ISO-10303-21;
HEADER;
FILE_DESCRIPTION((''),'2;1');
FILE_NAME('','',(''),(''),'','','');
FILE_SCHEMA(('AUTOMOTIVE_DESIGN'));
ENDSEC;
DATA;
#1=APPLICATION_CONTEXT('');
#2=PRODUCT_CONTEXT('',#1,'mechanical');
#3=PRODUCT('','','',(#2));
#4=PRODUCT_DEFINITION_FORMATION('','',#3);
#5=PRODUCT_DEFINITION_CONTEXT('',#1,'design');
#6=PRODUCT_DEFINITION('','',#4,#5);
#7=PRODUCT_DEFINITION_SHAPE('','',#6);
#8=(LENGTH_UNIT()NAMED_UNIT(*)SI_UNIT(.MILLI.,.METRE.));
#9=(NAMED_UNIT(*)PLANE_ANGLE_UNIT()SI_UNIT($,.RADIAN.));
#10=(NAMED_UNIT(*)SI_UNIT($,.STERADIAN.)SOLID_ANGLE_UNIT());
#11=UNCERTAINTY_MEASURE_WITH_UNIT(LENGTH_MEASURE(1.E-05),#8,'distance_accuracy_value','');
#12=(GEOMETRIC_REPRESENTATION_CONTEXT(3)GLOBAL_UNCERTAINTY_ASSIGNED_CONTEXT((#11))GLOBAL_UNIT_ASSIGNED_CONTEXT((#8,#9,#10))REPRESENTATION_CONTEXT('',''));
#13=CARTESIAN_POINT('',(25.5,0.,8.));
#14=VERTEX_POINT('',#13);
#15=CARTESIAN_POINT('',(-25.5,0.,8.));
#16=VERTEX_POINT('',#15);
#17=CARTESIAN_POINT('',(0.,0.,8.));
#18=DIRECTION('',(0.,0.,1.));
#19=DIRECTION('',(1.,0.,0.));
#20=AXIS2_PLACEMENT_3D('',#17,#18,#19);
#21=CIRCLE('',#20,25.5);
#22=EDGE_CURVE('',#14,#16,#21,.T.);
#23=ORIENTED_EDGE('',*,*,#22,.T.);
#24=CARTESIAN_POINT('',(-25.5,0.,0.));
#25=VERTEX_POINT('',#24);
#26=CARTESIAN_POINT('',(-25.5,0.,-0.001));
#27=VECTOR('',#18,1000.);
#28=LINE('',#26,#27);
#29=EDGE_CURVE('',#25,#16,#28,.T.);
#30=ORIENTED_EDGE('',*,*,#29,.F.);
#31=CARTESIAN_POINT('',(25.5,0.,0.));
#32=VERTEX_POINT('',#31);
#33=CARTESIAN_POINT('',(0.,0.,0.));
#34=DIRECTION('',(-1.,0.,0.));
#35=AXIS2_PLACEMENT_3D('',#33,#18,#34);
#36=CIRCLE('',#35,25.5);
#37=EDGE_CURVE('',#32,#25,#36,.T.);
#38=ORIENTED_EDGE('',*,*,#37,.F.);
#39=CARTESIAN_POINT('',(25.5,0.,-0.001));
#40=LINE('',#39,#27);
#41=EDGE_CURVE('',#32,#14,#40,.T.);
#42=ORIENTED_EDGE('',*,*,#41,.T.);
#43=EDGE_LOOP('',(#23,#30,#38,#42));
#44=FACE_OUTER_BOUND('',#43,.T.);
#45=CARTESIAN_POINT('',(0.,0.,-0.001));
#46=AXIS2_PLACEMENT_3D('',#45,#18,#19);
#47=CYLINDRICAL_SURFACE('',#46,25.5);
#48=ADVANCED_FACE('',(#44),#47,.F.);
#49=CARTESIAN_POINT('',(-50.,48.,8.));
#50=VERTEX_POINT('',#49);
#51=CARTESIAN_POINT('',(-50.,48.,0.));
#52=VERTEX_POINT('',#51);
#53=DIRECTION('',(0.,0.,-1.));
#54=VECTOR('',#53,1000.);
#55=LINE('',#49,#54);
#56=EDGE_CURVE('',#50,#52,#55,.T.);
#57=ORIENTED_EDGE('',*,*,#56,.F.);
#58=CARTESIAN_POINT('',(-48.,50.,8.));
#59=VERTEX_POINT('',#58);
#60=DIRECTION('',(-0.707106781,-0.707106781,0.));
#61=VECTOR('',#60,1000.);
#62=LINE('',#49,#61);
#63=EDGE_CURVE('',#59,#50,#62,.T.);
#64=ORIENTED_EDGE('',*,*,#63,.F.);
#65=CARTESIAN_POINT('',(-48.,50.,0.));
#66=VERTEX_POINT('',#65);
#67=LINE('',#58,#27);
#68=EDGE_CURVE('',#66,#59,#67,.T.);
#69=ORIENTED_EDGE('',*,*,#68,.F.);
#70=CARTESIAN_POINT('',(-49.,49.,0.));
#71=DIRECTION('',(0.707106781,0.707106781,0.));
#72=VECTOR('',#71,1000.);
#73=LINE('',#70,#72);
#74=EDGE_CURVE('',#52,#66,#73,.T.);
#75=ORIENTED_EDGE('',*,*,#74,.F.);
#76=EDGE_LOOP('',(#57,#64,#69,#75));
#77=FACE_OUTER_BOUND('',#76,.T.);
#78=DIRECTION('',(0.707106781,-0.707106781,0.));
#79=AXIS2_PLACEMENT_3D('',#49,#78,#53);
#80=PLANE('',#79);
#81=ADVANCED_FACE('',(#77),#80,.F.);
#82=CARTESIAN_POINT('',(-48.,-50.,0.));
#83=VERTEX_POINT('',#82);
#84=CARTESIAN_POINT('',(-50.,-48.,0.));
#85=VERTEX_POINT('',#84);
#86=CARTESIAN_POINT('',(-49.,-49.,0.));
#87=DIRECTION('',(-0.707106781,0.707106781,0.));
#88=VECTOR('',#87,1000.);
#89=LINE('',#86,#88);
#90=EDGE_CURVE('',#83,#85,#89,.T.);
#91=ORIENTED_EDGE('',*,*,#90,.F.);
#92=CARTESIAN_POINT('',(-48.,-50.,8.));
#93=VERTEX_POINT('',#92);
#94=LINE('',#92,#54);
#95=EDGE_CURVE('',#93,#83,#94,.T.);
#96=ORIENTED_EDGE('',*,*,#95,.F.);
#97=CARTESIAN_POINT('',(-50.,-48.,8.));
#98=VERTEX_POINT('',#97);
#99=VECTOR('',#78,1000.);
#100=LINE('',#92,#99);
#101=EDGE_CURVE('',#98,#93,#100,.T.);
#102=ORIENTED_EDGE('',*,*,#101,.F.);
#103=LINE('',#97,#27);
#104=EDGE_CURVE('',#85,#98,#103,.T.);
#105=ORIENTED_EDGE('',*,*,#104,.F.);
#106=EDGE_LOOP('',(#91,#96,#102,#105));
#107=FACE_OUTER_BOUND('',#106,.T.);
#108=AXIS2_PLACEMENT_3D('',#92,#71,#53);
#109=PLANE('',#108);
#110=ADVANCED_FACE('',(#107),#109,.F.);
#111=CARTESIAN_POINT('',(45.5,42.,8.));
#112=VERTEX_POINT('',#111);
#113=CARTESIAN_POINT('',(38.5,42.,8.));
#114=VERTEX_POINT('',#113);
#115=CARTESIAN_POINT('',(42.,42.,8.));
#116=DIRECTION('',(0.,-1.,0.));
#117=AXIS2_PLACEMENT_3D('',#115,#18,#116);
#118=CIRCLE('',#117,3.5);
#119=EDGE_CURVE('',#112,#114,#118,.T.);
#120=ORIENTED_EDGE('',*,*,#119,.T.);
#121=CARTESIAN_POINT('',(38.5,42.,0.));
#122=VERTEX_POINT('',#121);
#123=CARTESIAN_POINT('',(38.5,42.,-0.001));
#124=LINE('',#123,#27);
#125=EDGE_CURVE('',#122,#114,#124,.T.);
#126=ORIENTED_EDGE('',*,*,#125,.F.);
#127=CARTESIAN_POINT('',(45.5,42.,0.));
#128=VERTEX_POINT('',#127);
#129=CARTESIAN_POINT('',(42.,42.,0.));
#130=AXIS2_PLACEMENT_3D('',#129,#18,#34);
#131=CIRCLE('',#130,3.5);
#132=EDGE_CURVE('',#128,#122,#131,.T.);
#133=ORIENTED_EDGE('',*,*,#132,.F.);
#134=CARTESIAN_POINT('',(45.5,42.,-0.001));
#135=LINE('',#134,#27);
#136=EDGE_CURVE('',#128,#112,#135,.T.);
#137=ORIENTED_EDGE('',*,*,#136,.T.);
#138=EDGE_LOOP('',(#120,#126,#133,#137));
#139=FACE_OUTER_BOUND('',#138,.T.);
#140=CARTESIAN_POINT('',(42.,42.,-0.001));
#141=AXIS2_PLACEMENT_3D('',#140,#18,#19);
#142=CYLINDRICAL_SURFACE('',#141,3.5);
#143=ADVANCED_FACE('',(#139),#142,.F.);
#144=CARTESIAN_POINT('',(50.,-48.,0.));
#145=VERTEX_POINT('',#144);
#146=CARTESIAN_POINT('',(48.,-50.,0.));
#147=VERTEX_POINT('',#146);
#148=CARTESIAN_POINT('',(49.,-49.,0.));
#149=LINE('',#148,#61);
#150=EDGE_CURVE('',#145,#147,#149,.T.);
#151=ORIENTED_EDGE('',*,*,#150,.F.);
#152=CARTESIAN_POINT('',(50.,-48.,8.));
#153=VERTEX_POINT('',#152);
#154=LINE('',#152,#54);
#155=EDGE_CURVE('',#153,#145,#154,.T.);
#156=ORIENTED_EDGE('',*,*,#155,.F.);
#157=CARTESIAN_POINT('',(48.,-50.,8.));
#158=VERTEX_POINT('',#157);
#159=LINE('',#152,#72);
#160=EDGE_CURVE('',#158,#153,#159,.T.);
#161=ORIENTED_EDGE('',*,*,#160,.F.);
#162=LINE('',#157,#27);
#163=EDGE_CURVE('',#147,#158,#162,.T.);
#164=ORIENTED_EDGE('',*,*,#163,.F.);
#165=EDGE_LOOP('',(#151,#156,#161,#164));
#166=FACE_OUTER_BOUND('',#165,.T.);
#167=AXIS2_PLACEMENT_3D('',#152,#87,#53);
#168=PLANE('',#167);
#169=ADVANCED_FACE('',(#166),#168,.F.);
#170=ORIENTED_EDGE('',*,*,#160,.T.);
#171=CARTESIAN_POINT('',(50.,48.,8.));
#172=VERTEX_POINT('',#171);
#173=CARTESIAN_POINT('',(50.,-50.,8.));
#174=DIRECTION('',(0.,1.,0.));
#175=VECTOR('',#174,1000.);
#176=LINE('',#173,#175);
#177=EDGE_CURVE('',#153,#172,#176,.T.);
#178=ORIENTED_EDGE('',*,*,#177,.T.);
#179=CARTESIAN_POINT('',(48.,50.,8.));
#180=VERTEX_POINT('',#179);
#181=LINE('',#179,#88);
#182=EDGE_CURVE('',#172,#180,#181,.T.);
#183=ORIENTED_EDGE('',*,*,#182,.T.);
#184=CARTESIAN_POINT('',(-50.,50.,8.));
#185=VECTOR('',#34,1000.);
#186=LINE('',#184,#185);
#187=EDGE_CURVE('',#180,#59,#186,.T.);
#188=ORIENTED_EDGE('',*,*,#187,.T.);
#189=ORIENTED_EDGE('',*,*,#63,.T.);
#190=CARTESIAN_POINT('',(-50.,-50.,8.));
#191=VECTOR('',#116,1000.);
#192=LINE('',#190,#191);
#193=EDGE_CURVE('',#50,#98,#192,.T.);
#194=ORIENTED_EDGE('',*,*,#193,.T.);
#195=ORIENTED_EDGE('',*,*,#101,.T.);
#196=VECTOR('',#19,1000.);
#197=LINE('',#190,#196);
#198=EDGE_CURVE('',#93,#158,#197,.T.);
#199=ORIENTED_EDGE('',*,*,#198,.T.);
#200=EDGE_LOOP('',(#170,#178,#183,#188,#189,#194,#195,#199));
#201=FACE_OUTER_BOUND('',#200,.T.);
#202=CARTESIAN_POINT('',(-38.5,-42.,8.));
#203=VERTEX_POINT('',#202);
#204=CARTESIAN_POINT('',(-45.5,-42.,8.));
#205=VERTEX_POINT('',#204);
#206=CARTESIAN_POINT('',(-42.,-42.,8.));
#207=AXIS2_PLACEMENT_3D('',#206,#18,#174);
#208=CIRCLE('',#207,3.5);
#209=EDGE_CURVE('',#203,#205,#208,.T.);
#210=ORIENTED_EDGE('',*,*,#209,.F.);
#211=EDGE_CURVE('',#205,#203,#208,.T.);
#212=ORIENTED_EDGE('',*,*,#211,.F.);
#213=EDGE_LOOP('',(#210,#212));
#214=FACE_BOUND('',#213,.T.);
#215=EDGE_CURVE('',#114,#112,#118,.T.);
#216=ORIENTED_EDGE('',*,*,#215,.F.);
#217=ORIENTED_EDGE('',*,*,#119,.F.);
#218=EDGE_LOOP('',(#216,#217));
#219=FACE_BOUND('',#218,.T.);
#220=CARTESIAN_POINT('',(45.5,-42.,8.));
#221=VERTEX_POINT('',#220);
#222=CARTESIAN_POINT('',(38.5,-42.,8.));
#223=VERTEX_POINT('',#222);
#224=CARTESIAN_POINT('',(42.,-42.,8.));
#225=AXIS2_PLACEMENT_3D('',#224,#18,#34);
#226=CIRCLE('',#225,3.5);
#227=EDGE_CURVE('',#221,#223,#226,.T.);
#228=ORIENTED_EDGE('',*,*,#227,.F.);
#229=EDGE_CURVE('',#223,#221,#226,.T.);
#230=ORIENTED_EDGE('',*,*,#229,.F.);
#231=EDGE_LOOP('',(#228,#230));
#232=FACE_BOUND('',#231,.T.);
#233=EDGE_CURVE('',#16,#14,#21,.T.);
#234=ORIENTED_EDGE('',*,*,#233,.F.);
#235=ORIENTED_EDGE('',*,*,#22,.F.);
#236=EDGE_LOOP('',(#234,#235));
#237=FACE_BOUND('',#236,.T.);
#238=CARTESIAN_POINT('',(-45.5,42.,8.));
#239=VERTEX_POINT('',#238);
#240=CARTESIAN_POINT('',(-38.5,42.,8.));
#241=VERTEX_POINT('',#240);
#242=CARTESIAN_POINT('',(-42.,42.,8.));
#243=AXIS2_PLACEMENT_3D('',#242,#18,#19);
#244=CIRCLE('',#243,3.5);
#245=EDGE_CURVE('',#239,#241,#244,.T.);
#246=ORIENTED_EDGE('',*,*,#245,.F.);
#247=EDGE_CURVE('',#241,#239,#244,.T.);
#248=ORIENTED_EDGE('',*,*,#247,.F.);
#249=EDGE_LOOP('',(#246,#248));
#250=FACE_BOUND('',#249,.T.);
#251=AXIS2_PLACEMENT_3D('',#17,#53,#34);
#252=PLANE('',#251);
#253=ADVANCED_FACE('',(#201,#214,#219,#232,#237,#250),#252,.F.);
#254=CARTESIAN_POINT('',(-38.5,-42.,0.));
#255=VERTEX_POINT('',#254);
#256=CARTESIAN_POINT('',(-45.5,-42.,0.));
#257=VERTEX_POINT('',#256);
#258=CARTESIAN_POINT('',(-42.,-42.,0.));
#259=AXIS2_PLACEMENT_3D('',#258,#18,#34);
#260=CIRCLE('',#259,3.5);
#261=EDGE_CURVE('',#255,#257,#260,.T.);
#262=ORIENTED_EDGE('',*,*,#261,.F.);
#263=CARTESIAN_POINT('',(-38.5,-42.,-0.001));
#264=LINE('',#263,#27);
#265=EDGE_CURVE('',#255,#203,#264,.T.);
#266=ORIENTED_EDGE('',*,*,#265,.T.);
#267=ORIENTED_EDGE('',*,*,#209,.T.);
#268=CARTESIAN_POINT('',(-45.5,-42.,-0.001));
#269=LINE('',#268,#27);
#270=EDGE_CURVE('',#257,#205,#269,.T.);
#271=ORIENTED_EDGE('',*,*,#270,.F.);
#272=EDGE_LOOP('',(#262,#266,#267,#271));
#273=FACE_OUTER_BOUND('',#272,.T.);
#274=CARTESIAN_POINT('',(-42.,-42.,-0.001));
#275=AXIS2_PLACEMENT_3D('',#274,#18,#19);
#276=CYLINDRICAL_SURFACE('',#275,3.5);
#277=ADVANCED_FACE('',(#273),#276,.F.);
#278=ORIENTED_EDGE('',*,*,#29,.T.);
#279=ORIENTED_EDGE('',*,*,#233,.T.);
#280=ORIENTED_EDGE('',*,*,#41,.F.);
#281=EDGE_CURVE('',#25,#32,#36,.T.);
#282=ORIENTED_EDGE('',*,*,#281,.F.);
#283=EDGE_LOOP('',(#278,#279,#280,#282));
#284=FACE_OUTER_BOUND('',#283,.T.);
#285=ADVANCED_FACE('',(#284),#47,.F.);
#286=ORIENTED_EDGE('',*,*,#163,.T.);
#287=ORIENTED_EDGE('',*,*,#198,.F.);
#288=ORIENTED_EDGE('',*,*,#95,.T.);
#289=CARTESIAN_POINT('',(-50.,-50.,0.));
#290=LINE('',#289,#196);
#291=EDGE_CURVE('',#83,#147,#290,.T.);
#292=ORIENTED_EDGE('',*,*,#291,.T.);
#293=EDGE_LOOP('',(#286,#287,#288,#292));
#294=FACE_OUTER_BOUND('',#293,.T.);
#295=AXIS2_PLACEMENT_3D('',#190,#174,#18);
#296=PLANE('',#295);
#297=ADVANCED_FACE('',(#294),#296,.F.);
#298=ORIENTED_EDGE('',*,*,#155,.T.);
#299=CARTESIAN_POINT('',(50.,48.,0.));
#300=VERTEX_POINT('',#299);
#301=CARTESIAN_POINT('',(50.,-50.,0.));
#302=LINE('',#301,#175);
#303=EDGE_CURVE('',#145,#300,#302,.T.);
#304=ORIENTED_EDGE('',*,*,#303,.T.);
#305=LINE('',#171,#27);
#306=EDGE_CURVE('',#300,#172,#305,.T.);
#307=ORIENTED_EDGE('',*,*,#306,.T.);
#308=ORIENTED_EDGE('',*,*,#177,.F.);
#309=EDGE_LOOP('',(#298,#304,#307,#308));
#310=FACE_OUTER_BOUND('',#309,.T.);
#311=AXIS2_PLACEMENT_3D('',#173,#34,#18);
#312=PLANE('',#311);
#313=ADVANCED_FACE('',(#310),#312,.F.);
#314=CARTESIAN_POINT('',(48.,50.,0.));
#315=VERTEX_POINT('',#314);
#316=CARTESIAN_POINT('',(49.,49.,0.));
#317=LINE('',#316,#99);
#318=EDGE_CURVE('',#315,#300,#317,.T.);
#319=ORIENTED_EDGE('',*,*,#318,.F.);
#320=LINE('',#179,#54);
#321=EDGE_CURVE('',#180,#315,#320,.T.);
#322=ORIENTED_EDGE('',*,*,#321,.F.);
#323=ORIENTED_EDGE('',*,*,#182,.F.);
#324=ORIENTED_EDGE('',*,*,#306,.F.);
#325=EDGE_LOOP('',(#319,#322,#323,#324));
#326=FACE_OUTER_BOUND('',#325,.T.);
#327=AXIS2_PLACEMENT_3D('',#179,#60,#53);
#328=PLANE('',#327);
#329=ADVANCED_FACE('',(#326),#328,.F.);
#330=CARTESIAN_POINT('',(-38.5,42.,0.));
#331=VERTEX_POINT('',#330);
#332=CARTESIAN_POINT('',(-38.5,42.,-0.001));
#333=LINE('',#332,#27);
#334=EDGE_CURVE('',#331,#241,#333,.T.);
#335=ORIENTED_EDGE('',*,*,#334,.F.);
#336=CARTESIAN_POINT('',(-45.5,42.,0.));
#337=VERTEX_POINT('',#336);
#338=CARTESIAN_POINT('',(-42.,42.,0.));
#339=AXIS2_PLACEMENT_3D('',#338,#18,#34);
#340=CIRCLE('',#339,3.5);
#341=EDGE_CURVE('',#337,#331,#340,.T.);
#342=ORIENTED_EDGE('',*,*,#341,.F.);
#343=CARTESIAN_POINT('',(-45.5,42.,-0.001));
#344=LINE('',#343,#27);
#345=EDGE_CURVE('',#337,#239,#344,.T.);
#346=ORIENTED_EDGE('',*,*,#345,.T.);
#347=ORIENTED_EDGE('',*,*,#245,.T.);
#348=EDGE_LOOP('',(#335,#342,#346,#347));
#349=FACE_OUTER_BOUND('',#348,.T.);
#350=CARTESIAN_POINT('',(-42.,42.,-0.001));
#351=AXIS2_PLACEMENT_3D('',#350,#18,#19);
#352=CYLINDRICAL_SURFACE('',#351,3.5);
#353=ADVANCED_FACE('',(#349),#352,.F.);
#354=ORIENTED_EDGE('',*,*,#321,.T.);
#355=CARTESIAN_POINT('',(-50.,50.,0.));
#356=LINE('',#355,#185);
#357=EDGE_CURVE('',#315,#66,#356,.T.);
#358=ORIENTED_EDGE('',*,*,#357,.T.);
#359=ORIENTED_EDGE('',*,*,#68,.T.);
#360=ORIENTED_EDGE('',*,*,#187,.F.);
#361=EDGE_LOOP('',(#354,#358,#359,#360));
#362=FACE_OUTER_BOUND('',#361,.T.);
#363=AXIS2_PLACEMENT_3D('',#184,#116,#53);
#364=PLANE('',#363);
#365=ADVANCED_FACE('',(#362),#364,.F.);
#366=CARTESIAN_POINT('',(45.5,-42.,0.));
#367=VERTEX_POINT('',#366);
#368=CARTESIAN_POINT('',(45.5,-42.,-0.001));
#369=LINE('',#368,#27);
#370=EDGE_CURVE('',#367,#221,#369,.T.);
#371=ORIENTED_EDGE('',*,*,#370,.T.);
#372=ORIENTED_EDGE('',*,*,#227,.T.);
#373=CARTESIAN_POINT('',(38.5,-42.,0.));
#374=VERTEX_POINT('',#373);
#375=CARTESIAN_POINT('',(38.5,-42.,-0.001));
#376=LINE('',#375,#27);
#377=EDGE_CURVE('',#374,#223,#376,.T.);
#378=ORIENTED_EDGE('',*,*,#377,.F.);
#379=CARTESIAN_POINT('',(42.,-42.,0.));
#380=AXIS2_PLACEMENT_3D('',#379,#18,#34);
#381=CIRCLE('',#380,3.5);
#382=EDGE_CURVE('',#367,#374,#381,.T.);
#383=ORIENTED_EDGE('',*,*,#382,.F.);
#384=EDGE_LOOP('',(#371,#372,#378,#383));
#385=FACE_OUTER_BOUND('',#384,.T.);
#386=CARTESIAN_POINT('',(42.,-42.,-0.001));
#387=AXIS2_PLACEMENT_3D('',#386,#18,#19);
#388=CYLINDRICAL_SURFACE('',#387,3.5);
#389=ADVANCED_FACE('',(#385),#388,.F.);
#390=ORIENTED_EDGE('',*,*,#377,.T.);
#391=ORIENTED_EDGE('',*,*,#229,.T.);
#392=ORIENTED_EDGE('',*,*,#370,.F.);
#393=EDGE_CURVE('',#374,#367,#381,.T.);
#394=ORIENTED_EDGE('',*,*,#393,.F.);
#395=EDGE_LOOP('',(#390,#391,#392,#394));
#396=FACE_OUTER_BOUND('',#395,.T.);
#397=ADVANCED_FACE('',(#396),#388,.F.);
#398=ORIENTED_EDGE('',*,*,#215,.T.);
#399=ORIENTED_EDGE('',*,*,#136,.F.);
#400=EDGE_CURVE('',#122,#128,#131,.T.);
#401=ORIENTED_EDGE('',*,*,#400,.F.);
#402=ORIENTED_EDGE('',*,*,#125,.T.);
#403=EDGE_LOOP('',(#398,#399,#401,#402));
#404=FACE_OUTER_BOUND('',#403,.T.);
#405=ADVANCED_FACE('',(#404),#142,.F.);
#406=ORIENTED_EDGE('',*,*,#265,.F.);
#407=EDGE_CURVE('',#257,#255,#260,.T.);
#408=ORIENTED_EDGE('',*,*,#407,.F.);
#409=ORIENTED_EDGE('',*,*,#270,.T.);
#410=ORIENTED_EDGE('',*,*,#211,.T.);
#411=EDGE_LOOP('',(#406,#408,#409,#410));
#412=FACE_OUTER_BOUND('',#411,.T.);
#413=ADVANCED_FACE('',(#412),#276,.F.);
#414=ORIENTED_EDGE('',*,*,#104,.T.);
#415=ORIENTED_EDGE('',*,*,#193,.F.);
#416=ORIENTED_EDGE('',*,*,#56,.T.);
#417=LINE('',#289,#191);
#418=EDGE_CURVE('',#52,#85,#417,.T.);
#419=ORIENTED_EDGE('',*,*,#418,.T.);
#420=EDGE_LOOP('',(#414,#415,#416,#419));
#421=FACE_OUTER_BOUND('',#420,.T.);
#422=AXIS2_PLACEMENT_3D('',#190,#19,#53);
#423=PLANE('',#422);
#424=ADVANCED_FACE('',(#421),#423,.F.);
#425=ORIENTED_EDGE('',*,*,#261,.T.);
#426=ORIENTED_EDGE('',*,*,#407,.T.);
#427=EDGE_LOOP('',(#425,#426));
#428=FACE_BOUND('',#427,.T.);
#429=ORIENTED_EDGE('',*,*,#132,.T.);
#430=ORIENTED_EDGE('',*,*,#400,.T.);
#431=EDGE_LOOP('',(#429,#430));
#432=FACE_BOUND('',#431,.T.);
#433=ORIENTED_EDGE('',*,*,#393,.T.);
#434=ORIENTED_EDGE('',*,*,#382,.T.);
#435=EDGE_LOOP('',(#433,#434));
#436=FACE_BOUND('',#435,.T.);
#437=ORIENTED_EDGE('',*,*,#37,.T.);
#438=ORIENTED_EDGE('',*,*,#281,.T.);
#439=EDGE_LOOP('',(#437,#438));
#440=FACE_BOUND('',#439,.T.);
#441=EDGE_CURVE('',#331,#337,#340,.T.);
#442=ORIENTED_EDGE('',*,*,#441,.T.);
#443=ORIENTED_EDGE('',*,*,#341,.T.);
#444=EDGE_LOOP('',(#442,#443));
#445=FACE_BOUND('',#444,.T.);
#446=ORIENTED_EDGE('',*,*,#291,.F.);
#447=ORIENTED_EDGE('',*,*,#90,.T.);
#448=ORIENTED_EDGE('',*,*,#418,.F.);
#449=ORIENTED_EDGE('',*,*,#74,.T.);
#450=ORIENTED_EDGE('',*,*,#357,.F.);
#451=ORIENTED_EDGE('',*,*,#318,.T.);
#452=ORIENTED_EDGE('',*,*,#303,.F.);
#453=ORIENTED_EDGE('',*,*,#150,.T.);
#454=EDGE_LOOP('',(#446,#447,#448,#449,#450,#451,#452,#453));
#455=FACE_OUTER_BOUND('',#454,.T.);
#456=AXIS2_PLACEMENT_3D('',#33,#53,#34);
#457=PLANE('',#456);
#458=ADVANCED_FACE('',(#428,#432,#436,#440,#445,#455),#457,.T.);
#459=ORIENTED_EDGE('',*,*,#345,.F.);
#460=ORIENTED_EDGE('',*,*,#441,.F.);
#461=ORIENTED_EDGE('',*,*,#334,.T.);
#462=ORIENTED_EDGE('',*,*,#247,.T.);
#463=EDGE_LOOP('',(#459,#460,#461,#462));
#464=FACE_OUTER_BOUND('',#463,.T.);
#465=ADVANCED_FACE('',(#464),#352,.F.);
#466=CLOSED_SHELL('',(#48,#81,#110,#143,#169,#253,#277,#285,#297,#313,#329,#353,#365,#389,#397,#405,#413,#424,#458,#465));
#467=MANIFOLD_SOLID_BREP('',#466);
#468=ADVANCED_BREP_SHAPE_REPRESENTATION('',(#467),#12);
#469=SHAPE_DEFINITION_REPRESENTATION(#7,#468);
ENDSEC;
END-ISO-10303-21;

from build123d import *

# Parameters (mm, degrees)
SKETCH_1_W               = 100
SKETCH_1_H               = 100
EXTRUDE_1_DEPTH          = 8
CUT_EXTRUDE_1_REACH      = 73.162
SKETCH_2_R               = 25.5
CUT_EXTRUDE_2_REACH      = 73.162
SKETCH_3_R               = 3.5
PATTERN_CIRCULAR_1_COUNT = 4
CHAMFER_1_SIZE           = 2


with BuildPart() as part:
    # 草图1 → 凸台-拉伸1 (new body)
    with BuildSketch(Plane.XY):
        Rectangle(SKETCH_1_W, SKETCH_1_H)
    extrude(amount=EXTRUDE_1_DEPTH)

    # 草图2 → 切除-拉伸1 (cut, up to next)
    with BuildSketch(Plane.XY.offset(8), mode=Mode.PRIVATE) as cut_extrude_1_sk1:
        Circle(SKETCH_2_R)
    cut_extrude_1_tool1 = extrude(cut_extrude_1_sk1.sketch, amount=-CUT_EXTRUDE_1_REACH, mode=Mode.PRIVATE) & part.part
    add(cut_extrude_1_tool1.solids().sort_by_distance((0, 0, 8))[0], mode=Mode.SUBTRACT)

    # 草图3 → 切除-拉伸2 (cut, up to next)
    with BuildSketch(Plane.XY.offset(8), mode=Mode.PRIVATE) as cut_extrude_2_sk1:
        with Locations((-42, 42)):
            Circle(SKETCH_3_R)
    cut_extrude_2_tool1 = extrude(cut_extrude_2_sk1.sketch, amount=-CUT_EXTRUDE_2_REACH, mode=Mode.PRIVATE) & part.part
    cut_extrude_2 = cut_extrude_2_tool1.solids().sort_by_distance((-42, 42, 8))[0]
    add(cut_extrude_2, mode=Mode.SUBTRACT)

    # 阵列(圆周)1: 切除-拉伸2 ×4 about axis
    pattern_circular_1_axis = Axis((0, 0, 0), (0, 0, 1))
    for i in range(1, PATTERN_CIRCULAR_1_COUNT):
        add(cut_extrude_2.rotate(pattern_circular_1_axis, i * 360 / PATTERN_CIRCULAR_1_COUNT), mode=Mode.SUBTRACT)

    # 倒角1
    chamfer_1_edges = [part.edges().sort_by_distance(p)[0] for p in [
        (50, -50, 4),
        (-50, -50, 4),
        (-50, 50, 4),
        (50, 50, 4),
    ]]
    chamfer(chamfer_1_edges, length=CHAMFER_1_SIZE)


solid = part.part
